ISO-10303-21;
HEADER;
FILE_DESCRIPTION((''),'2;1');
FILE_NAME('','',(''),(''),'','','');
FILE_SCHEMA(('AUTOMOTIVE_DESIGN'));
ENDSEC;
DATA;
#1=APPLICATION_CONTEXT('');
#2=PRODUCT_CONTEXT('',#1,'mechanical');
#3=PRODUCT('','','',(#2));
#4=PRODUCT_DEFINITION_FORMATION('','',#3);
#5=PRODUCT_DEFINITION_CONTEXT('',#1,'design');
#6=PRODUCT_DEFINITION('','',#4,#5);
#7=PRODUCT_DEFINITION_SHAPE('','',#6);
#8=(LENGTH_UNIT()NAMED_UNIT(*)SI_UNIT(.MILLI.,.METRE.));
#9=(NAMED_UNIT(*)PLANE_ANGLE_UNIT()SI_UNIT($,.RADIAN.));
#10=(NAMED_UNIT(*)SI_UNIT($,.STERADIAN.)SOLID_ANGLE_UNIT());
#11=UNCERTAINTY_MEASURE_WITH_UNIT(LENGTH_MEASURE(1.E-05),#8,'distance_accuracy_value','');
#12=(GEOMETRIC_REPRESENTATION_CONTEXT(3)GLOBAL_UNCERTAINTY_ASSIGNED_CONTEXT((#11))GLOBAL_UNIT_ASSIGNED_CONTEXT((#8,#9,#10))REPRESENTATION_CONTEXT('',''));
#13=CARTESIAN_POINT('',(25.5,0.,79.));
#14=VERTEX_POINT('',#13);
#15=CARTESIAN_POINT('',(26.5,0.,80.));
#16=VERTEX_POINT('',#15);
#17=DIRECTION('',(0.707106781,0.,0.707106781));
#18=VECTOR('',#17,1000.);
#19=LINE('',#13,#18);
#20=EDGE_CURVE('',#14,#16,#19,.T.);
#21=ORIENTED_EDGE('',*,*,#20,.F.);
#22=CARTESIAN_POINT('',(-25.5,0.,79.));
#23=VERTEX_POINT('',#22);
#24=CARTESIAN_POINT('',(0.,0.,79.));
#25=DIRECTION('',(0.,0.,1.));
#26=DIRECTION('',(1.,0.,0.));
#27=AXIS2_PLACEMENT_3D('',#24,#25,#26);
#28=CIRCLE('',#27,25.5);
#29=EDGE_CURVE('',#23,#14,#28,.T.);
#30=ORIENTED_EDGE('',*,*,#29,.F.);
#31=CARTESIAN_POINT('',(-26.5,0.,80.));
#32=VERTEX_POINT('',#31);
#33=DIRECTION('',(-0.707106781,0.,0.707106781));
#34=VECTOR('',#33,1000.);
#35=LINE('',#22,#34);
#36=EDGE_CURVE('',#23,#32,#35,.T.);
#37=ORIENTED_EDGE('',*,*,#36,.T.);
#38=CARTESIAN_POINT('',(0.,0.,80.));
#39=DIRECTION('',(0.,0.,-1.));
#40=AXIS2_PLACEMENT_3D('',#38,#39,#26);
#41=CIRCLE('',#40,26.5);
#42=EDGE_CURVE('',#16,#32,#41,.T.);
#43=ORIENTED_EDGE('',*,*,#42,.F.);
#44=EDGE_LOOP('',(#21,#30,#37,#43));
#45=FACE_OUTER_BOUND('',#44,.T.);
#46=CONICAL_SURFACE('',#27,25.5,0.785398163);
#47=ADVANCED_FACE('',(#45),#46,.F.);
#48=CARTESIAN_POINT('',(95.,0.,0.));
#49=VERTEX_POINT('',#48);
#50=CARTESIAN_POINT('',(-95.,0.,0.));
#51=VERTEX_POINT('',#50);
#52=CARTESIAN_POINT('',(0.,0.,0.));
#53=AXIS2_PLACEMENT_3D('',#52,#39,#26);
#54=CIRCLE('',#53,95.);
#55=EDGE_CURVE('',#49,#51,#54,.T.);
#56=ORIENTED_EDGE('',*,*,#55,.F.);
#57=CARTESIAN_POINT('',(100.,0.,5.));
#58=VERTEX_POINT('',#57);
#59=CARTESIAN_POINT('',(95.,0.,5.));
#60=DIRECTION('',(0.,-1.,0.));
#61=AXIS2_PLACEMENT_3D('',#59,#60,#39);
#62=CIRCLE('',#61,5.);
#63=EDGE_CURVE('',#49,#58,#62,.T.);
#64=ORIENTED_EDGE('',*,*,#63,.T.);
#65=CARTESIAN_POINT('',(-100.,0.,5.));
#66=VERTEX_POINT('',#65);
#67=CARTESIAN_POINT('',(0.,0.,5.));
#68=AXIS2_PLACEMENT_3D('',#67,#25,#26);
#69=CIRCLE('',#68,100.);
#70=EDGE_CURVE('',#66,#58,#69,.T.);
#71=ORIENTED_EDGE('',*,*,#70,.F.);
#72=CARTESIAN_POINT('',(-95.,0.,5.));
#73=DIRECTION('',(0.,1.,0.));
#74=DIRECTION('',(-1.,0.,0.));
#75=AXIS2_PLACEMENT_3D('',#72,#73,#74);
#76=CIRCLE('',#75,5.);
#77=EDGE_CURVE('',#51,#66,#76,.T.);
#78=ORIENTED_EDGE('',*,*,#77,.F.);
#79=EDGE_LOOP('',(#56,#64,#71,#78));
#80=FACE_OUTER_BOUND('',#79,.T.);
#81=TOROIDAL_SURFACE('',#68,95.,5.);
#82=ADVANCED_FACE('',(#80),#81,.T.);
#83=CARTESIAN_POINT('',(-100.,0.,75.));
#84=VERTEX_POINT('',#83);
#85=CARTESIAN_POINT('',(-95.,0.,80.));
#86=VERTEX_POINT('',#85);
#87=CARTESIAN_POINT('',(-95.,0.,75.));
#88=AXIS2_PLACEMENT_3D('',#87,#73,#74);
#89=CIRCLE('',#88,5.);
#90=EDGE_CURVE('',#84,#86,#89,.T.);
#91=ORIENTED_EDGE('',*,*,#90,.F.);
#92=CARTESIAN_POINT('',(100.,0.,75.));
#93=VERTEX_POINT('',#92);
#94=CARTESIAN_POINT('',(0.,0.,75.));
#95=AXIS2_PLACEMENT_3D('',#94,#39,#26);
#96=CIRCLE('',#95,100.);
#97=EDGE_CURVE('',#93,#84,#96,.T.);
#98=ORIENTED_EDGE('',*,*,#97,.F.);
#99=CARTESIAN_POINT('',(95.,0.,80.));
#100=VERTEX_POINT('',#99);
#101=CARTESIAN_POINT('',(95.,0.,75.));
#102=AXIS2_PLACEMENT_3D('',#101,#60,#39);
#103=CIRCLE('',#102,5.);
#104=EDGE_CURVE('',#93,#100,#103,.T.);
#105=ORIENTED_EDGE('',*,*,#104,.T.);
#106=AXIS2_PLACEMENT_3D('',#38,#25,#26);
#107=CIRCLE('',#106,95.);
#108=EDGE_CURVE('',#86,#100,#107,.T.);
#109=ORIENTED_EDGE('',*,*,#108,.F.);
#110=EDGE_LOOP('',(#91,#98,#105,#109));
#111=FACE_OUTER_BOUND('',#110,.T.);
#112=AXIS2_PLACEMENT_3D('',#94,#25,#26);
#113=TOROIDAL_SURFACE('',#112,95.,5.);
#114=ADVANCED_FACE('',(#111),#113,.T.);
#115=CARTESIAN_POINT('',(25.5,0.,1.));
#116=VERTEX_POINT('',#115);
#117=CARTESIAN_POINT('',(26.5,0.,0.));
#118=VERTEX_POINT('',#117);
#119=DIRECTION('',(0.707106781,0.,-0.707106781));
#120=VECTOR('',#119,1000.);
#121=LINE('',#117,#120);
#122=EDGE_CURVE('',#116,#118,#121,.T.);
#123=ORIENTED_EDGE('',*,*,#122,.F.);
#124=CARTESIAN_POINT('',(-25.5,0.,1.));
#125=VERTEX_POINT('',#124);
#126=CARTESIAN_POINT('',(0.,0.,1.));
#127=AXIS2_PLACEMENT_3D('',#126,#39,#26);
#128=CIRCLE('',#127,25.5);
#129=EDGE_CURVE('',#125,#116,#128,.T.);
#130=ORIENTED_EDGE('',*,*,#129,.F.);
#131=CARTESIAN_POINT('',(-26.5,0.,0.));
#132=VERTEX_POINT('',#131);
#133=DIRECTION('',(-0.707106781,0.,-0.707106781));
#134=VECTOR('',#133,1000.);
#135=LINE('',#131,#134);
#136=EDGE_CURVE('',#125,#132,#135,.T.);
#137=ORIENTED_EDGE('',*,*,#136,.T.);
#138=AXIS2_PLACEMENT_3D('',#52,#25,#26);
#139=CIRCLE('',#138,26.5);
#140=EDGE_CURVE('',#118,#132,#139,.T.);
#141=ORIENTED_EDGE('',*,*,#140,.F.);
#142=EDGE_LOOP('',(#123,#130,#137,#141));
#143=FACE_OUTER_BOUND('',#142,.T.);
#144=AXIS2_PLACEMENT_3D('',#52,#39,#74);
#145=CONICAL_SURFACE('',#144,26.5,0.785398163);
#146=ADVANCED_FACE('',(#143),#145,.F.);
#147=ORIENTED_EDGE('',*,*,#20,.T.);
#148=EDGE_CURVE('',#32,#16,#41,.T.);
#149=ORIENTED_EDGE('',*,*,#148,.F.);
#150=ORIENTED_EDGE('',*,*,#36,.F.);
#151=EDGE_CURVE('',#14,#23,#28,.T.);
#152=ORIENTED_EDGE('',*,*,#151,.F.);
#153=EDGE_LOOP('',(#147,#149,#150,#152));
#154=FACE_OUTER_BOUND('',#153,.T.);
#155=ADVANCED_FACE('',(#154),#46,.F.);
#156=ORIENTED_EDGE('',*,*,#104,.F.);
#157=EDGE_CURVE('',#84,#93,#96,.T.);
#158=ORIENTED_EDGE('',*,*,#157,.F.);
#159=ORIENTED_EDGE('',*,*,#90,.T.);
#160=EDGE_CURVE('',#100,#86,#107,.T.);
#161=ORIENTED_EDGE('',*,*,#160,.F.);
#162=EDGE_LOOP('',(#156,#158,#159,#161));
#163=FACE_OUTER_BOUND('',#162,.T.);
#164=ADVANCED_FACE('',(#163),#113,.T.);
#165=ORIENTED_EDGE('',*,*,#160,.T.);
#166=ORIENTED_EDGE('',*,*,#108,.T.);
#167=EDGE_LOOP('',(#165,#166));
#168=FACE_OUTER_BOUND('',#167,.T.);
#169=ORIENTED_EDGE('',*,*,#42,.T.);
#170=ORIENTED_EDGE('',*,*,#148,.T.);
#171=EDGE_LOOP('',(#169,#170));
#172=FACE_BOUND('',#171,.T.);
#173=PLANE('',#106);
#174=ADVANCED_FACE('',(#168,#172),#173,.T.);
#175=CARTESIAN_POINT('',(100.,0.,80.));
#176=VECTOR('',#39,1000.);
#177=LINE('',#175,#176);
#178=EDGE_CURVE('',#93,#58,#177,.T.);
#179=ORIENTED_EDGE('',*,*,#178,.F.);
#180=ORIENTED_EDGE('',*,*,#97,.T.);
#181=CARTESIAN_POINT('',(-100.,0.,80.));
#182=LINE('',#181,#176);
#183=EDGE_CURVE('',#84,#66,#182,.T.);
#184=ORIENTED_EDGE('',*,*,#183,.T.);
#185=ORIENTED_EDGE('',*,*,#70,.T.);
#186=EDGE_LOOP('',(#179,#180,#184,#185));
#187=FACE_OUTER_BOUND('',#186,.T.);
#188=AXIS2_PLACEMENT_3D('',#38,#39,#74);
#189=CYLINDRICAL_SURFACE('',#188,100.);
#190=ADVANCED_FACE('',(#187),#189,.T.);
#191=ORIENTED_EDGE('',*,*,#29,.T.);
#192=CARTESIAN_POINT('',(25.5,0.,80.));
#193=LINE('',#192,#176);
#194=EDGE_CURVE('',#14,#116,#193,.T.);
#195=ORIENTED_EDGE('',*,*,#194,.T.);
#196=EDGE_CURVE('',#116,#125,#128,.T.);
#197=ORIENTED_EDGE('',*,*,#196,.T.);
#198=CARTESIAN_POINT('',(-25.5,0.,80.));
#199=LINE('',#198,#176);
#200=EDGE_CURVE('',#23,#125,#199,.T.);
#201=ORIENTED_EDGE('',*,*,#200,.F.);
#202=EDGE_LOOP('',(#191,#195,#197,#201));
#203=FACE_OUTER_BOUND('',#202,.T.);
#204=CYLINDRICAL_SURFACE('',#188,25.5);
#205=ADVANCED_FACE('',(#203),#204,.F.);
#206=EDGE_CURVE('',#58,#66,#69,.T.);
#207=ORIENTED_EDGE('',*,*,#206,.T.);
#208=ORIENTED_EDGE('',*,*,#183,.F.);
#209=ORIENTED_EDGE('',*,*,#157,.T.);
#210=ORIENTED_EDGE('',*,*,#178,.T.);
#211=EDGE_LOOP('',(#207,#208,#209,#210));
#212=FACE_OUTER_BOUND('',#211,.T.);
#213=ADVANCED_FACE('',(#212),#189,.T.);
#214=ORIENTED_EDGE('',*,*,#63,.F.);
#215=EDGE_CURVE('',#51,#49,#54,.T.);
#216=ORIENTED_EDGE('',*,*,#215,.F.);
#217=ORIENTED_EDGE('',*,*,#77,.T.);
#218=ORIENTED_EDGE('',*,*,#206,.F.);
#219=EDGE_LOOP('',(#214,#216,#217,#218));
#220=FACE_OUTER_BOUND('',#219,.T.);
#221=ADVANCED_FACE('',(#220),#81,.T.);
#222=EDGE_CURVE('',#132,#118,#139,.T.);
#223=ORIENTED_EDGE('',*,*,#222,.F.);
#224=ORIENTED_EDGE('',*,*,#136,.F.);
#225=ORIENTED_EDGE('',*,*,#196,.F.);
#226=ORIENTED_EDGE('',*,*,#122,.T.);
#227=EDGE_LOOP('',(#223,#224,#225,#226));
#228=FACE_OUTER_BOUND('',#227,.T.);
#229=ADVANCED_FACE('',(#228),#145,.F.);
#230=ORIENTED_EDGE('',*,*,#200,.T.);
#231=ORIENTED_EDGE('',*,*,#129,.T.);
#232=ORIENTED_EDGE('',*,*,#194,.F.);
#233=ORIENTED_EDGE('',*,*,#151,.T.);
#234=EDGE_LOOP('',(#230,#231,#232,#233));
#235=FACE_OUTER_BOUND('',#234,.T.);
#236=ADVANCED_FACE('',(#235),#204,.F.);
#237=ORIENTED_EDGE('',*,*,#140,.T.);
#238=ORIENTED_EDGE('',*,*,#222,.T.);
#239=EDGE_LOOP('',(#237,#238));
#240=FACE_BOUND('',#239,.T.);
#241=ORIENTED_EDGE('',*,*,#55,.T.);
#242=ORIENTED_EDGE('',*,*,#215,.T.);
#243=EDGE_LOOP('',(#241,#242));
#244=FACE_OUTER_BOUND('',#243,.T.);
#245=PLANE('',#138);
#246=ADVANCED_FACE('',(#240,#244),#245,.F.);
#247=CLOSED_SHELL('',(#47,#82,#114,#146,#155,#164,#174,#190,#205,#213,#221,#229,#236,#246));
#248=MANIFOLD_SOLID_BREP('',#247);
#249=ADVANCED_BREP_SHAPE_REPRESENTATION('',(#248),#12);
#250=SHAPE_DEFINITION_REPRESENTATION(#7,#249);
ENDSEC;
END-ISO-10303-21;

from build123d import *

# Parameters (mm, degrees)
SKETCH1_R           = 100
SKETCH1_R_2         = 25.5
BOSS_EXTRUDE1_DEPTH = 80
FILLET1_R           = 5
CHAMFER1_SIZE       = 1


with BuildPart() as part:
    # Sketch1 → Boss-Extrude1 (new body)
    with BuildSketch(Plane.XY):
        Circle(SKETCH1_R)
        Circle(SKETCH1_R_2, mode=Mode.SUBTRACT)
    extrude(amount=BOSS_EXTRUDE1_DEPTH)

    # Fillet1
    fillet1_edges = [part.edges().sort_by_distance(p)[0] for p in [
        (-100, 0, 0),
        (-100, 0, 80),
    ]]
    fillet(fillet1_edges, radius=FILLET1_R)

    # Chamfer1
    chamfer1_edges = [part.edges().sort_by_distance(p)[0] for p in [
        (-25.5, 0, 0),
        (-25.5, 0, 80),
    ]]
    chamfer(chamfer1_edges, length=CHAMFER1_SIZE)


solid = part.part
